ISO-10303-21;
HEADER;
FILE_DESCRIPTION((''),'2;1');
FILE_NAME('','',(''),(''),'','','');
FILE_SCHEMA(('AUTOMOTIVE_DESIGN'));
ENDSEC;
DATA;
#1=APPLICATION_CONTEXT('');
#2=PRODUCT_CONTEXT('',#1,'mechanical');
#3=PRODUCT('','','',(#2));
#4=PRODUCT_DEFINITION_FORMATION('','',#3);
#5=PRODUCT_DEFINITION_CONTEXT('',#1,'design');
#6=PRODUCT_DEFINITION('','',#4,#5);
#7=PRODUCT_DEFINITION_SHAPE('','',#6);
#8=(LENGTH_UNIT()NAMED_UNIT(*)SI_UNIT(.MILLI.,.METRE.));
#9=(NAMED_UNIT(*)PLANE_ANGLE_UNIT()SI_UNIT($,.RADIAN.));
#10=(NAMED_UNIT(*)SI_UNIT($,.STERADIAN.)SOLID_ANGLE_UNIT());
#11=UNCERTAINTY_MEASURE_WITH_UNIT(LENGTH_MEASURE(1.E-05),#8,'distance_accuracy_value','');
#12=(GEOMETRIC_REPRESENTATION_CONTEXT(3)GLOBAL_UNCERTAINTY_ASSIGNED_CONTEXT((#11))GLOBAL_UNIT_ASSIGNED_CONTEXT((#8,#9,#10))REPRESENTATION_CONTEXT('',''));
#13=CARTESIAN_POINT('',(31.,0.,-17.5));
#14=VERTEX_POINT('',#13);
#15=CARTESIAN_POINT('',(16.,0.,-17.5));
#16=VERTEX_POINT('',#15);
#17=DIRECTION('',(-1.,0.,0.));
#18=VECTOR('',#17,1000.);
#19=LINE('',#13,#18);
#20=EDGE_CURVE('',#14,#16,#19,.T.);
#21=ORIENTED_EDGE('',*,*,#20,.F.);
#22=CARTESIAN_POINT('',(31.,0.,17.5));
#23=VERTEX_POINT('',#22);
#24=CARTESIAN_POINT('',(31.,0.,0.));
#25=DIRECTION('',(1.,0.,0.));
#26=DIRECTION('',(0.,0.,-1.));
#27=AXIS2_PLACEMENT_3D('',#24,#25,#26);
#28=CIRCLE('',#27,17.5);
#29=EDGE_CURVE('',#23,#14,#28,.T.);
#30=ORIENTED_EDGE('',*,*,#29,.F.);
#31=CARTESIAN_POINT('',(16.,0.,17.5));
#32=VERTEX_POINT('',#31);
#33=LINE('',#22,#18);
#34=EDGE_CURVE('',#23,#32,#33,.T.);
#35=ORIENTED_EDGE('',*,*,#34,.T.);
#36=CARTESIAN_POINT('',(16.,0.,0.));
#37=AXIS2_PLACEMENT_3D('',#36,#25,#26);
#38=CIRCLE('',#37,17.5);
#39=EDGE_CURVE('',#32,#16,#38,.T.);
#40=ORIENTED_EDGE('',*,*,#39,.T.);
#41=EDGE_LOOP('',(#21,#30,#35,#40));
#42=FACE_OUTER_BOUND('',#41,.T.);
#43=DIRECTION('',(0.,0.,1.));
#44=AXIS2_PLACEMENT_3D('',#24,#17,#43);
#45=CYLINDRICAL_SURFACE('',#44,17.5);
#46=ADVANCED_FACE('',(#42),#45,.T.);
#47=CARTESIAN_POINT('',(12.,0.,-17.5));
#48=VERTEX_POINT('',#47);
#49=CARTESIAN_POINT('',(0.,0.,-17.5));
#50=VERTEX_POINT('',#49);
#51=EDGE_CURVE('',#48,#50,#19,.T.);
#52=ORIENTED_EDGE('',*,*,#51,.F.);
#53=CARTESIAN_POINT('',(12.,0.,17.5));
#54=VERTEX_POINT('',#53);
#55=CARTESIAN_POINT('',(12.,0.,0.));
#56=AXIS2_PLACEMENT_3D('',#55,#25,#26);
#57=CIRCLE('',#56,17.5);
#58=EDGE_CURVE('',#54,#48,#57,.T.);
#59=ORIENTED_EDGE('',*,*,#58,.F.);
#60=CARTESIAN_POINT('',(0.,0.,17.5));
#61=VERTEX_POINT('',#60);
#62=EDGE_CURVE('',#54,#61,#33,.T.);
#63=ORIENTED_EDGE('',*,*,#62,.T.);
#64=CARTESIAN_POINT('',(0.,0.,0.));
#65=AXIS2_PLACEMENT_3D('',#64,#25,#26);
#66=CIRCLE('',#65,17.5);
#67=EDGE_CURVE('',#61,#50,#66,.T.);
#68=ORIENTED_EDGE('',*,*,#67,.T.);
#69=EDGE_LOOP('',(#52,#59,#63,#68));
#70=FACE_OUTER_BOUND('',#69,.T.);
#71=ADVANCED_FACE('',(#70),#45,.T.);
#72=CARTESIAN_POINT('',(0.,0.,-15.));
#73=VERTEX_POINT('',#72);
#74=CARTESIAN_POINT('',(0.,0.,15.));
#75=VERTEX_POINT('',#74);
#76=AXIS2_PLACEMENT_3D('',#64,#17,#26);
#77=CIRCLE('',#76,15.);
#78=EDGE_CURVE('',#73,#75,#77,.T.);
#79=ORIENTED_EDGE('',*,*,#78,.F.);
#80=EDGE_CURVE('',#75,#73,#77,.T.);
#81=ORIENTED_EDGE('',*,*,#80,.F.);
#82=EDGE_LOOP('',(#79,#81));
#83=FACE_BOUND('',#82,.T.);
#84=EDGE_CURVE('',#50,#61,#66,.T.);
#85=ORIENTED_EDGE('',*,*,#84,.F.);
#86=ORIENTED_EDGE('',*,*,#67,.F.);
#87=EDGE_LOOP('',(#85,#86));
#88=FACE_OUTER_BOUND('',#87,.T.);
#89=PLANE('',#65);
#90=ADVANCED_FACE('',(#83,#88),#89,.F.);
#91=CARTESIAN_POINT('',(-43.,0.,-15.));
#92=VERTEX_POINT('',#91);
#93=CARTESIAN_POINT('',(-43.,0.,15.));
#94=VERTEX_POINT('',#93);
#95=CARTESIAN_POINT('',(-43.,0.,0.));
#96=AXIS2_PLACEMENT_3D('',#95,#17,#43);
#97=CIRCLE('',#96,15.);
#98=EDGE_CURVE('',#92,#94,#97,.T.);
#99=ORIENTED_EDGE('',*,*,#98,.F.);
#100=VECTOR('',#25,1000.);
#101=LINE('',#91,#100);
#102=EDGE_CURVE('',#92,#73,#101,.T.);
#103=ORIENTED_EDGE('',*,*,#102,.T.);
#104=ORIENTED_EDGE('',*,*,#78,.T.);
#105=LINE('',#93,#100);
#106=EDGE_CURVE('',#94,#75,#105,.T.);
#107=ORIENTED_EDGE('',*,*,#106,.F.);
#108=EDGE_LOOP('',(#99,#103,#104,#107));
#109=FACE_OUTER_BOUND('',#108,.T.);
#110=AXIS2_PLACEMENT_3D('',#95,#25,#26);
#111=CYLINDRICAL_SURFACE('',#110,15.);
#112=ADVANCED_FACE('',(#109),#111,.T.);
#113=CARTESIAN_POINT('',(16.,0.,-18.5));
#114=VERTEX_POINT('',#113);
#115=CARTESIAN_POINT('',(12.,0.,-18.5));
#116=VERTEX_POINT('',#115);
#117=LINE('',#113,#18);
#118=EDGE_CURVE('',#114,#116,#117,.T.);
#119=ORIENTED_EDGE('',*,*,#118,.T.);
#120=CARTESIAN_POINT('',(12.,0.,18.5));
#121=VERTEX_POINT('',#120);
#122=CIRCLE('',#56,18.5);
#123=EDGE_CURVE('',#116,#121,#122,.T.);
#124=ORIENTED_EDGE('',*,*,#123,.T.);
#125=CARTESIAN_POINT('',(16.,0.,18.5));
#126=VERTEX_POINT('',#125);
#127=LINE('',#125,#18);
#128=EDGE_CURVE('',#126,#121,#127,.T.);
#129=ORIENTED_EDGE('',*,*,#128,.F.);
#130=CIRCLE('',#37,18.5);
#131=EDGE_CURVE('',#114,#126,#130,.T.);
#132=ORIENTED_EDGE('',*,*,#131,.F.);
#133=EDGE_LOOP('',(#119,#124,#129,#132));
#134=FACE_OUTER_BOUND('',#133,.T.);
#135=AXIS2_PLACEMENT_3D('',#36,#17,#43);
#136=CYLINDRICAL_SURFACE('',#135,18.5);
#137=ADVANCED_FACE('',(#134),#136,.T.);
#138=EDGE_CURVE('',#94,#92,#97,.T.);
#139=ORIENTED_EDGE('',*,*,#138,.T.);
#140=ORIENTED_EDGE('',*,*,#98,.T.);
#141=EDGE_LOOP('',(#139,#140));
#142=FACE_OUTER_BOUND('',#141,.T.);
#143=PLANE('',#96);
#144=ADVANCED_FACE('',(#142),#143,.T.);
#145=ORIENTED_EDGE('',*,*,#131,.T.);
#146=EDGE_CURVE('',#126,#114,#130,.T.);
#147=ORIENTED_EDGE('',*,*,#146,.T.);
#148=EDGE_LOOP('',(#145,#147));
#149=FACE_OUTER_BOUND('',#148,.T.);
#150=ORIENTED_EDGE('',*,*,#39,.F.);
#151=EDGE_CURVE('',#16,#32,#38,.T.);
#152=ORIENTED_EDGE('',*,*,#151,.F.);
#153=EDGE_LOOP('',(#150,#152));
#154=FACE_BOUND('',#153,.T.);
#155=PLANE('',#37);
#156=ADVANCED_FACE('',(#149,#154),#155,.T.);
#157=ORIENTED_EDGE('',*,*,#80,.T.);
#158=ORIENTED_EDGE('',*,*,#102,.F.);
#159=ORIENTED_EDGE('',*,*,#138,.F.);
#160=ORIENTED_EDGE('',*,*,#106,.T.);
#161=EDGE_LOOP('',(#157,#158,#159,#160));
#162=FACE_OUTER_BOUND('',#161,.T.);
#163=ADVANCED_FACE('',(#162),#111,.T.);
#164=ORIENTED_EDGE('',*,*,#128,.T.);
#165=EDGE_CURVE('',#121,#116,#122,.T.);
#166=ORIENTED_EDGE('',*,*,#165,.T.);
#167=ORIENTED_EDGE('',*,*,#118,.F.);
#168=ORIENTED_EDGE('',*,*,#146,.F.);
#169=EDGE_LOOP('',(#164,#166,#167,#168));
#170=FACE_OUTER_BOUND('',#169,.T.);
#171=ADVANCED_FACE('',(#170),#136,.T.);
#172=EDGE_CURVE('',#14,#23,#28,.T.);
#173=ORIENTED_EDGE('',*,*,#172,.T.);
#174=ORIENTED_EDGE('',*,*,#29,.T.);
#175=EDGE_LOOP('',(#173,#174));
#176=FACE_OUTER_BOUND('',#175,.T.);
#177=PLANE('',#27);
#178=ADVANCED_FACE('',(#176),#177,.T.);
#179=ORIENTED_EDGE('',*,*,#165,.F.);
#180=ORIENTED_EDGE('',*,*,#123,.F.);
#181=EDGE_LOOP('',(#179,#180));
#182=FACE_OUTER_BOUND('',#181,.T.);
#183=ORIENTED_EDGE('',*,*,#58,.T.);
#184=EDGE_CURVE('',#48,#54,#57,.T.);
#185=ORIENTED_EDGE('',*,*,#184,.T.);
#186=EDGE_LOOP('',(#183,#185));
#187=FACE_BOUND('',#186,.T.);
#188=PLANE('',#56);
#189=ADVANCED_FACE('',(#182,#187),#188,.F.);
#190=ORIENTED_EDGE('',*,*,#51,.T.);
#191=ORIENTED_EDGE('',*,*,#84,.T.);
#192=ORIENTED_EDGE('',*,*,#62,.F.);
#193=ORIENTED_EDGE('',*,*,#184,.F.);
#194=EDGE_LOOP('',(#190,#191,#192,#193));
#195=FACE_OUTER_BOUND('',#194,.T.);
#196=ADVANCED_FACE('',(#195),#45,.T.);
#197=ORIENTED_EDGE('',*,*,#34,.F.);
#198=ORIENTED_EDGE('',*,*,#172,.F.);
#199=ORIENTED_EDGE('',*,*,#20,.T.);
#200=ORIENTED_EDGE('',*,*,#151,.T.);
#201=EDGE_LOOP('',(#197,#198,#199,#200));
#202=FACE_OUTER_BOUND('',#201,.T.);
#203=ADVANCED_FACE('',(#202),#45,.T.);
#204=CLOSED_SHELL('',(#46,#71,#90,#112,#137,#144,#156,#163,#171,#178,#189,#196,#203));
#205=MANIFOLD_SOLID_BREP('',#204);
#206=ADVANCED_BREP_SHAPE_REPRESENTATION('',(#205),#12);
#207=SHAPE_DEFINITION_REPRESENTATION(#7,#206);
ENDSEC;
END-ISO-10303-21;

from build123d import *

# Parameters (mm, degrees)
SKETCH_1_R      = 17.5
EXTRUDE_1_DEPTH = 31
SKETCH_2_R      = 15
EXTRUDE_2_DEPTH = 43
SKETCH_4_R      = 18.5
EXTRUDE_3_DEPTH = 4


with BuildPart() as part:
    # 草图1 → 凸台-拉伸1 (new body)
    with BuildSketch(Plane(origin=(0, 0, 0), x_dir=(0, 0, -1), z_dir=(1, 0, 0))):
        Circle(SKETCH_1_R)
    extrude(amount=EXTRUDE_1_DEPTH)

    # 草图2 → 凸台-拉伸2 (add)
    with BuildSketch(Plane.ZY):
        with Locations(Location((0, 0, 0), (0, 0, 180))):
            Circle(SKETCH_2_R)
    extrude(amount=EXTRUDE_2_DEPTH)

    # 草图4 → 凸台-拉伸3 (add)
    with BuildSketch(Plane(origin=(12, 0, 0), x_dir=(0, 0, -1), z_dir=(1, 0, 0))):
        Circle(SKETCH_4_R)
    extrude(amount=EXTRUDE_3_DEPTH)


solid = part.part
